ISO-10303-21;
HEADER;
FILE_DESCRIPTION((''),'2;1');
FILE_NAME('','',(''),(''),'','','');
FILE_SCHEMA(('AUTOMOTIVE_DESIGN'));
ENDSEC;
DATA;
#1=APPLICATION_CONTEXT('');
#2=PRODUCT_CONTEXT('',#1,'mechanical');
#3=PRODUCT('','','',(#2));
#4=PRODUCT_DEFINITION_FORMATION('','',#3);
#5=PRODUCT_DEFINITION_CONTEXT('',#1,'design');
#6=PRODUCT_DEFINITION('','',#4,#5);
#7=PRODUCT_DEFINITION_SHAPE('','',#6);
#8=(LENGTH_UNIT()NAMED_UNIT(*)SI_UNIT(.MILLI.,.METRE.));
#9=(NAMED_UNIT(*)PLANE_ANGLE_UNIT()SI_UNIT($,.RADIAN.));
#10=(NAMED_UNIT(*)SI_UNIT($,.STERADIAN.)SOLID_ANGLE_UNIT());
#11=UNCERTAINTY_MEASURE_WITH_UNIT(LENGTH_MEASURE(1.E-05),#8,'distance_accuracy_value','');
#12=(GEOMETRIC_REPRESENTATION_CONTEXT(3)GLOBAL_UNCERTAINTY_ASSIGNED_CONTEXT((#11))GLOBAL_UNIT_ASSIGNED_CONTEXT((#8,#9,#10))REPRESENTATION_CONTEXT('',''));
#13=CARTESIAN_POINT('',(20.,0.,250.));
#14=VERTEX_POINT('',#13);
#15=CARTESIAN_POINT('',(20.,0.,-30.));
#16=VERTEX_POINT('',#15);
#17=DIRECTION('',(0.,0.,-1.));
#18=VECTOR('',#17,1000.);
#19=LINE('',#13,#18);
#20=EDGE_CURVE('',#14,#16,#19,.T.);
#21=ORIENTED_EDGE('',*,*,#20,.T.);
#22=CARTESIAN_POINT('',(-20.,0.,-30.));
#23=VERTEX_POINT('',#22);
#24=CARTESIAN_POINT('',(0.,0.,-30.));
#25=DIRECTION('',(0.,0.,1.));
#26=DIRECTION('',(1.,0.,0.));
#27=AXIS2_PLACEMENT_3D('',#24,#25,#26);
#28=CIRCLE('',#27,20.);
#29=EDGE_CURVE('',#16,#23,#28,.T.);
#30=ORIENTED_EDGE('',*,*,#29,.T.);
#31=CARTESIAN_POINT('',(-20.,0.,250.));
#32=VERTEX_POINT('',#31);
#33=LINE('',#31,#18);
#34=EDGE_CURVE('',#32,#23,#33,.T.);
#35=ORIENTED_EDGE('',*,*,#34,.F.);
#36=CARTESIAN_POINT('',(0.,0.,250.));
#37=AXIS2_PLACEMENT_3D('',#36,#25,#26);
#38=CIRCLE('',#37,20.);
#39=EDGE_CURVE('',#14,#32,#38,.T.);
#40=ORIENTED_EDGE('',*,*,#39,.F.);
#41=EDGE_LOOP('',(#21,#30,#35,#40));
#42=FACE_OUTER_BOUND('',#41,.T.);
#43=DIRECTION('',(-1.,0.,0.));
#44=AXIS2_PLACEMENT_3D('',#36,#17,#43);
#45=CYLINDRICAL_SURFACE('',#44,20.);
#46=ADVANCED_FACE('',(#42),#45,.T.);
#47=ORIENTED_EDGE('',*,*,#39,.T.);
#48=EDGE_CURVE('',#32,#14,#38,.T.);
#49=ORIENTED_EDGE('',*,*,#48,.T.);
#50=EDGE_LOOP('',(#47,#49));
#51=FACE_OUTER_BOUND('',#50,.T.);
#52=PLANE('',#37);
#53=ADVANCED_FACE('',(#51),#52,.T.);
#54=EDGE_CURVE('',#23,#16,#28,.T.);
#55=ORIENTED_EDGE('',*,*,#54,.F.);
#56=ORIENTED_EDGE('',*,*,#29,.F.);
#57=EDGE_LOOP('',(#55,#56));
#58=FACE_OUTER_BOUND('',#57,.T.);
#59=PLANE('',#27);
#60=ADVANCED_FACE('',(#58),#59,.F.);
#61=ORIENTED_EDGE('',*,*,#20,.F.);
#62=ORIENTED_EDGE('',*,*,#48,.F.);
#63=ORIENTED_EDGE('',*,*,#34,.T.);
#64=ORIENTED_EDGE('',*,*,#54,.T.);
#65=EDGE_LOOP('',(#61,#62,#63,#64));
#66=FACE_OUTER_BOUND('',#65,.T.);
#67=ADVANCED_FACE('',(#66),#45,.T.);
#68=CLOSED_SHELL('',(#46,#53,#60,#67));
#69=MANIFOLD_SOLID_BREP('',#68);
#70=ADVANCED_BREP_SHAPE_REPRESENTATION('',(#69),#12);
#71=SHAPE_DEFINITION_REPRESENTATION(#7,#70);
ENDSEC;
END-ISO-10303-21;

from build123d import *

# Parameters (mm, degrees)
BOSS_EXTRUDE1_DEPTH      = 250
BOSS_EXTRUDE1_DEPTH_BACK = 30
SKETCH1_R                = 20


with BuildPart() as part:
    # Sketch1 → Boss-Extrude1 (new, two sides: drawn at the far end of the back side and taken through both)
    with BuildSketch(Plane.XY.offset(-BOSS_EXTRUDE1_DEPTH_BACK)):
        Circle(SKETCH1_R)
    extrude(amount=BOSS_EXTRUDE1_DEPTH + BOSS_EXTRUDE1_DEPTH_BACK)


solid = part.part
